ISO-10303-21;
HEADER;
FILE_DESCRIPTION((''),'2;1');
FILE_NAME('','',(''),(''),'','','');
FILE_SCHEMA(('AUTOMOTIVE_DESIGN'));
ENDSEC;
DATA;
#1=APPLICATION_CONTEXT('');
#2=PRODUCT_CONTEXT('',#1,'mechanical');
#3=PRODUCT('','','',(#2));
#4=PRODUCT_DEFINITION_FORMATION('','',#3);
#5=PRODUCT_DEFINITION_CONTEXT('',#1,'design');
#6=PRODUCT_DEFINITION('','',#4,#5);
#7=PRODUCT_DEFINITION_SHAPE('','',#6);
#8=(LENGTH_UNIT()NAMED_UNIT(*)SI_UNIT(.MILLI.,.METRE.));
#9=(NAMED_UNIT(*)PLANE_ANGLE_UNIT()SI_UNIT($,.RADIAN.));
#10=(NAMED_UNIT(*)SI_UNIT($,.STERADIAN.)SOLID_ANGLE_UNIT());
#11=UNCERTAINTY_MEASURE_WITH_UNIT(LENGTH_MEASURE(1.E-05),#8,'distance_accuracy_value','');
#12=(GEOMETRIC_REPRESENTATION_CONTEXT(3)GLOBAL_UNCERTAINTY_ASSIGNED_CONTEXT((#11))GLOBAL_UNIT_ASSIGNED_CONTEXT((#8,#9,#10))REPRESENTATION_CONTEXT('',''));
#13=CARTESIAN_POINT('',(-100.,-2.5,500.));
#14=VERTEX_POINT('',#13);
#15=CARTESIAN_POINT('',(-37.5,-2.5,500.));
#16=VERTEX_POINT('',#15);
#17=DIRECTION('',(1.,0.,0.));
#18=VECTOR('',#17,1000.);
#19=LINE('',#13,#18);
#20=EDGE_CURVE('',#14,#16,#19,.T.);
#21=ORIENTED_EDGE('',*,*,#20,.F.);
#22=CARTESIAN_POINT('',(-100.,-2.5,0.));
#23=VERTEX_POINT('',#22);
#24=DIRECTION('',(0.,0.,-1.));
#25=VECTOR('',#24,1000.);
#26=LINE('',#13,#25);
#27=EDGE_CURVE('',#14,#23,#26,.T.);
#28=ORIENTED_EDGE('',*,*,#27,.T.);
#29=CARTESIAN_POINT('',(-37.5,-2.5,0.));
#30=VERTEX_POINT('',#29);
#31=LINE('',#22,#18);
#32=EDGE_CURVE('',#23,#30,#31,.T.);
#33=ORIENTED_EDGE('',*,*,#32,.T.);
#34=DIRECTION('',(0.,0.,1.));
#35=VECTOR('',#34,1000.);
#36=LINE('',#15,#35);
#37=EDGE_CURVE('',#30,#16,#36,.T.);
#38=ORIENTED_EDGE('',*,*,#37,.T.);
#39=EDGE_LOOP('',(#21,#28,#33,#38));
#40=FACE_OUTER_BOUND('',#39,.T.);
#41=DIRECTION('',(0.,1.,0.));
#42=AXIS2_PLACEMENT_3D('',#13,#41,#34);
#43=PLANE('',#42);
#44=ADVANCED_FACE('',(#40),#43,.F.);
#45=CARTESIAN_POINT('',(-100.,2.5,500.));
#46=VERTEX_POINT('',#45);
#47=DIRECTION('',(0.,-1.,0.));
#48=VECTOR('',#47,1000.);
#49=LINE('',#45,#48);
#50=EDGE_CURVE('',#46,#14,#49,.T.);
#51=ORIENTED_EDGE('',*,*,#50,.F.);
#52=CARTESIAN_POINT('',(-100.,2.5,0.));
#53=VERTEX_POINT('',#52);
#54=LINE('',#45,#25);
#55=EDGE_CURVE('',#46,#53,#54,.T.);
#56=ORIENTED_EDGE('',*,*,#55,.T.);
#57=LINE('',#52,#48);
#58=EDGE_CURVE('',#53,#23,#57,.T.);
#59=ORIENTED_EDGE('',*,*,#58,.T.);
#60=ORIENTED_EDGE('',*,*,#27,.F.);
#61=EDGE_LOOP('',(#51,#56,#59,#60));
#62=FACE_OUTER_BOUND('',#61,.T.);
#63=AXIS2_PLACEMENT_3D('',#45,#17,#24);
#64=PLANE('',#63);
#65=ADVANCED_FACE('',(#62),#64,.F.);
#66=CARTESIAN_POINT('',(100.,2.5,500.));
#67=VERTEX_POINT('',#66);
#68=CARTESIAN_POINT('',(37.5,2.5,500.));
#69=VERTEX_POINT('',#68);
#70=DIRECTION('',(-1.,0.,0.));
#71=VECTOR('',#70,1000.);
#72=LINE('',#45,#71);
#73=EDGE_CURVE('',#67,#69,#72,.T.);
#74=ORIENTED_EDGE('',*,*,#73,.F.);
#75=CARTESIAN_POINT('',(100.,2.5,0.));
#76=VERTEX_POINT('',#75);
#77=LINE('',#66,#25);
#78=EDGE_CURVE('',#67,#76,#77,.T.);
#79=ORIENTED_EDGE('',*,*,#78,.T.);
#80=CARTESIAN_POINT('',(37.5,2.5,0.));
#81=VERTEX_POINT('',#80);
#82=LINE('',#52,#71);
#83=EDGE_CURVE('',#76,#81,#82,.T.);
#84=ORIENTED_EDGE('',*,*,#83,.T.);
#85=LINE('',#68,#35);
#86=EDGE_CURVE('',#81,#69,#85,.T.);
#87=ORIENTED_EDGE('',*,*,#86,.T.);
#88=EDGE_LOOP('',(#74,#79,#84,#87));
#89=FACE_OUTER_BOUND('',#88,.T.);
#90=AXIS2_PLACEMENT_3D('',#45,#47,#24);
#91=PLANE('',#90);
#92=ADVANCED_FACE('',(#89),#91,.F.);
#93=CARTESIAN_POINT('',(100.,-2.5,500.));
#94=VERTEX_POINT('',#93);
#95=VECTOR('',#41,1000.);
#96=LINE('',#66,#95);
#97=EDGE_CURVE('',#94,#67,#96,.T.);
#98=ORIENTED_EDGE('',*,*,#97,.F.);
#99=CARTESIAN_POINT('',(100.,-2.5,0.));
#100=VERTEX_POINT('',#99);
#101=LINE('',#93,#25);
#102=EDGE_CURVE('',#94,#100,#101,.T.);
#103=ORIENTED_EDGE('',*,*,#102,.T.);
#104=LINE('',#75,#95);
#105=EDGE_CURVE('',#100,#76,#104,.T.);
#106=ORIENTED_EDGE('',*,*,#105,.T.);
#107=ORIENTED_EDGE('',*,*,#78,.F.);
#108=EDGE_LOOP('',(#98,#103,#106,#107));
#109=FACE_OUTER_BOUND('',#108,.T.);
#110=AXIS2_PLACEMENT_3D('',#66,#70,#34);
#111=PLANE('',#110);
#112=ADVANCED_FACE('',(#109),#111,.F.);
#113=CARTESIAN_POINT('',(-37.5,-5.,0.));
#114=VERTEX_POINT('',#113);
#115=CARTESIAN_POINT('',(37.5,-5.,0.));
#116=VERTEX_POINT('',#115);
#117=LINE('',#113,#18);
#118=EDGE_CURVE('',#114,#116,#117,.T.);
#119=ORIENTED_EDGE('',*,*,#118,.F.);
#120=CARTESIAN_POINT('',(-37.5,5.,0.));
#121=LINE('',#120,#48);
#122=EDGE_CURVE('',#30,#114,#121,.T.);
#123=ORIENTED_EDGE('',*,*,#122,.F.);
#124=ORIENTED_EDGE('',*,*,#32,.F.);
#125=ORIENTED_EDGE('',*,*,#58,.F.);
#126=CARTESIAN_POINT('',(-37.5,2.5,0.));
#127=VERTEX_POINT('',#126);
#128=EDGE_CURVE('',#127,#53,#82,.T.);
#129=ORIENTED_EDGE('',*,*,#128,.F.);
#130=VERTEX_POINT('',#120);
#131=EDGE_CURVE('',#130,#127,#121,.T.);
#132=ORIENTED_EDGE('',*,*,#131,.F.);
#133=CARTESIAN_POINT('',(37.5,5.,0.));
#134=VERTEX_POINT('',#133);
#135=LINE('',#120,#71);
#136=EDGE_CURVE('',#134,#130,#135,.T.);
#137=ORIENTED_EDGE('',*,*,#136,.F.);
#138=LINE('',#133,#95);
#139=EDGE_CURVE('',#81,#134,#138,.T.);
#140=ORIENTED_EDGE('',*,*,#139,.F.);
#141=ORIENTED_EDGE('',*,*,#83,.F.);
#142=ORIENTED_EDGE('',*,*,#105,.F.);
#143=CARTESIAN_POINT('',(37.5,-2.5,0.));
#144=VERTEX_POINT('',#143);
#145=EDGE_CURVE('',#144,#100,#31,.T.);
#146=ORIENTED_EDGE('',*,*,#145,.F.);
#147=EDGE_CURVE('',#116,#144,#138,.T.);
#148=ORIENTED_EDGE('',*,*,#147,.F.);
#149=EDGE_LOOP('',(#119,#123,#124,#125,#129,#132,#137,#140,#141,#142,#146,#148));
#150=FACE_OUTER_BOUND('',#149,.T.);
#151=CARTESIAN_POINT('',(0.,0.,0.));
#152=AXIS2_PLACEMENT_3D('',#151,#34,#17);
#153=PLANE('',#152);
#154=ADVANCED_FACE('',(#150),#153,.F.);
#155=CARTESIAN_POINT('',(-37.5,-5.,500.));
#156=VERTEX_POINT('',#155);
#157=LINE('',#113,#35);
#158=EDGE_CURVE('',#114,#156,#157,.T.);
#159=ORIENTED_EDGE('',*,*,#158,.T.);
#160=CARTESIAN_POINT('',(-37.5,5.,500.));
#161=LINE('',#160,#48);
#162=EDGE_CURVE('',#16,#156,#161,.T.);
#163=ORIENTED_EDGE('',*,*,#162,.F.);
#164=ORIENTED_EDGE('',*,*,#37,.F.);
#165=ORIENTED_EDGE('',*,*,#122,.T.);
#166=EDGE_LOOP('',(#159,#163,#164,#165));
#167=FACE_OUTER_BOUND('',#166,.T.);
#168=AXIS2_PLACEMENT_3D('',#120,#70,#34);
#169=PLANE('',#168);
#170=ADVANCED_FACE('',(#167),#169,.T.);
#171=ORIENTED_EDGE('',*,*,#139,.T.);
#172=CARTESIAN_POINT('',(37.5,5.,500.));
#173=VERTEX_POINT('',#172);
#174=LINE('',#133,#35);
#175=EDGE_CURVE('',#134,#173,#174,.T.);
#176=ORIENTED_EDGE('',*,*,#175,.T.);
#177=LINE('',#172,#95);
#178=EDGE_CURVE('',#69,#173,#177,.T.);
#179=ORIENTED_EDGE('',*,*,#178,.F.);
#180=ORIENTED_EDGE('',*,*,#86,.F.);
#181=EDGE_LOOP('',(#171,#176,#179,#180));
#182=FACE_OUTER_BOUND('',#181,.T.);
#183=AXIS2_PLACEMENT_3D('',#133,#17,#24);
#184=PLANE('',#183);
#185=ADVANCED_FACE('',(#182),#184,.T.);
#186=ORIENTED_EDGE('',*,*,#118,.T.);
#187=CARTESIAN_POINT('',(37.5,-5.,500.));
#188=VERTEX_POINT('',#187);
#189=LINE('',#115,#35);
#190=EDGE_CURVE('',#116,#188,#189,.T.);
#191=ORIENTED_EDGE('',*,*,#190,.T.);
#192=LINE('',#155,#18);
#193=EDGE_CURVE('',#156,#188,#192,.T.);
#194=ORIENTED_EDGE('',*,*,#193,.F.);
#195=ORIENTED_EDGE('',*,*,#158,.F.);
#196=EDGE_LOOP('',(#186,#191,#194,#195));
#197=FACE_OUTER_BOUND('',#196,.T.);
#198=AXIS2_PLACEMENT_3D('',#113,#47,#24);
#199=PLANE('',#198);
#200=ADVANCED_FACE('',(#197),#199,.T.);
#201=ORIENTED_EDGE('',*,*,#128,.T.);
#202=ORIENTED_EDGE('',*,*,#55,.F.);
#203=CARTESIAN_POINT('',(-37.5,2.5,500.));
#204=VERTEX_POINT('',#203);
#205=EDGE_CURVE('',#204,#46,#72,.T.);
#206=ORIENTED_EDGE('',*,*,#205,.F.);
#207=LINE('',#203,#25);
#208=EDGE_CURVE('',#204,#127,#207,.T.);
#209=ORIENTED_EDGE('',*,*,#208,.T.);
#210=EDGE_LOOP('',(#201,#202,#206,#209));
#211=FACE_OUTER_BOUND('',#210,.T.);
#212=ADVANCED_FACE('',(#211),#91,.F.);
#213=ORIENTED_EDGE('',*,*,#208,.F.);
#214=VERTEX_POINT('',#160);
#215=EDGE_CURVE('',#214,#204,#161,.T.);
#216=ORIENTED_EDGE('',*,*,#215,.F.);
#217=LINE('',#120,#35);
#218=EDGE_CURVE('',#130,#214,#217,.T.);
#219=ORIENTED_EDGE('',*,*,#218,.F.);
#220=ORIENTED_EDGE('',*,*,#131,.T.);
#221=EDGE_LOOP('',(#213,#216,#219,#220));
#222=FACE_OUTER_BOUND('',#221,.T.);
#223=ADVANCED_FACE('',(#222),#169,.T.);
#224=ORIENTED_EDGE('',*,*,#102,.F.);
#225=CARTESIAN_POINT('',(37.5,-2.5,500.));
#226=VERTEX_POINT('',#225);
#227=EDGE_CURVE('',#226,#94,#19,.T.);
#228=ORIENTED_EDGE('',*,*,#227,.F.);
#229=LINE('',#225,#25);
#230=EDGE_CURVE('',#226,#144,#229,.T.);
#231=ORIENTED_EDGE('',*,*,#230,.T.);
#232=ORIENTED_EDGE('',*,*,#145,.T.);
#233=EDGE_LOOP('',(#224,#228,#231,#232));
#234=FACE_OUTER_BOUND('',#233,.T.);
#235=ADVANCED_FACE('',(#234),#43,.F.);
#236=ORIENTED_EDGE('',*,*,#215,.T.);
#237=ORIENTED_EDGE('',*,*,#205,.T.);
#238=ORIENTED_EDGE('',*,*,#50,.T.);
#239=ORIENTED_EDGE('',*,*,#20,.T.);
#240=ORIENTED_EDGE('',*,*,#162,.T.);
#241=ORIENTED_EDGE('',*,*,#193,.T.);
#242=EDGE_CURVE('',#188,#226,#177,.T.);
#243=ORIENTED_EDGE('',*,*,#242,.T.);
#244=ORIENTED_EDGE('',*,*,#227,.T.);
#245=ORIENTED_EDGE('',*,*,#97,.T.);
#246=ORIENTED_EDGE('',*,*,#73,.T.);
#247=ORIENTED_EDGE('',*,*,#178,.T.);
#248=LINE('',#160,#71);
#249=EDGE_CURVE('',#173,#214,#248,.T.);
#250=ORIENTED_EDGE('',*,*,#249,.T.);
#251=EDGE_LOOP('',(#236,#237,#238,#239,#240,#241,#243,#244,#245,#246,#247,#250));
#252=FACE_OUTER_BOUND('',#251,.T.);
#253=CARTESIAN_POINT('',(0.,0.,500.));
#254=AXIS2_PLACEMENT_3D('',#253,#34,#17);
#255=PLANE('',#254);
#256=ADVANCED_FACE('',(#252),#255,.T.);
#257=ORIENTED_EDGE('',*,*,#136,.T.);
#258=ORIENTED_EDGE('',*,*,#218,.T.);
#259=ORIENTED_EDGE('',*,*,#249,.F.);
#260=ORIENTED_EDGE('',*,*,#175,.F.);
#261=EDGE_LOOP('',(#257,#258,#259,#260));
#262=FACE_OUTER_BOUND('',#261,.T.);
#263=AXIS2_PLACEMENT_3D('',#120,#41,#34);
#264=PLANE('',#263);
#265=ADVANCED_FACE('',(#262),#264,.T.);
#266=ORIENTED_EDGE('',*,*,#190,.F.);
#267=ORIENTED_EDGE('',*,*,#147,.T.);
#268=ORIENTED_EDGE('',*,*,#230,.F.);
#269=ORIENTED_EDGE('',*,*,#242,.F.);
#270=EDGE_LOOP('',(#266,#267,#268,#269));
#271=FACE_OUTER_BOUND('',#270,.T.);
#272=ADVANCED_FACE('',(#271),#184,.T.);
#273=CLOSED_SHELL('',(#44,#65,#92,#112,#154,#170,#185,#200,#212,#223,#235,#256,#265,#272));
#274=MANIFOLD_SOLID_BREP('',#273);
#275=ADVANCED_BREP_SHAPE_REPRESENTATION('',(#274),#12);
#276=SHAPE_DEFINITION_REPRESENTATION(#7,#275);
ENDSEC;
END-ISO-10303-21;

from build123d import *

# Parameters (mm, degrees)
SKETCH1_W           = 200
SKETCH1_H           = 5
BOSS_EXTRUDE1_DEPTH = 500
SKETCH2_W           = 75
SKETCH2_H           = 10
BOSS_EXTRUDE2_DEPTH = 500


with BuildPart() as part:
    # Sketch1 → Boss-Extrude1 (new body)
    with BuildSketch(Plane.XY):
        Rectangle(SKETCH1_W, SKETCH1_H)
    extrude(amount=BOSS_EXTRUDE1_DEPTH)

    # Sketch2 → Boss-Extrude2 (add)
    with BuildSketch(Plane.XY.offset(500)):
        Rectangle(SKETCH2_W, SKETCH2_H)
    extrude(amount=-BOSS_EXTRUDE2_DEPTH)


solid = part.part
